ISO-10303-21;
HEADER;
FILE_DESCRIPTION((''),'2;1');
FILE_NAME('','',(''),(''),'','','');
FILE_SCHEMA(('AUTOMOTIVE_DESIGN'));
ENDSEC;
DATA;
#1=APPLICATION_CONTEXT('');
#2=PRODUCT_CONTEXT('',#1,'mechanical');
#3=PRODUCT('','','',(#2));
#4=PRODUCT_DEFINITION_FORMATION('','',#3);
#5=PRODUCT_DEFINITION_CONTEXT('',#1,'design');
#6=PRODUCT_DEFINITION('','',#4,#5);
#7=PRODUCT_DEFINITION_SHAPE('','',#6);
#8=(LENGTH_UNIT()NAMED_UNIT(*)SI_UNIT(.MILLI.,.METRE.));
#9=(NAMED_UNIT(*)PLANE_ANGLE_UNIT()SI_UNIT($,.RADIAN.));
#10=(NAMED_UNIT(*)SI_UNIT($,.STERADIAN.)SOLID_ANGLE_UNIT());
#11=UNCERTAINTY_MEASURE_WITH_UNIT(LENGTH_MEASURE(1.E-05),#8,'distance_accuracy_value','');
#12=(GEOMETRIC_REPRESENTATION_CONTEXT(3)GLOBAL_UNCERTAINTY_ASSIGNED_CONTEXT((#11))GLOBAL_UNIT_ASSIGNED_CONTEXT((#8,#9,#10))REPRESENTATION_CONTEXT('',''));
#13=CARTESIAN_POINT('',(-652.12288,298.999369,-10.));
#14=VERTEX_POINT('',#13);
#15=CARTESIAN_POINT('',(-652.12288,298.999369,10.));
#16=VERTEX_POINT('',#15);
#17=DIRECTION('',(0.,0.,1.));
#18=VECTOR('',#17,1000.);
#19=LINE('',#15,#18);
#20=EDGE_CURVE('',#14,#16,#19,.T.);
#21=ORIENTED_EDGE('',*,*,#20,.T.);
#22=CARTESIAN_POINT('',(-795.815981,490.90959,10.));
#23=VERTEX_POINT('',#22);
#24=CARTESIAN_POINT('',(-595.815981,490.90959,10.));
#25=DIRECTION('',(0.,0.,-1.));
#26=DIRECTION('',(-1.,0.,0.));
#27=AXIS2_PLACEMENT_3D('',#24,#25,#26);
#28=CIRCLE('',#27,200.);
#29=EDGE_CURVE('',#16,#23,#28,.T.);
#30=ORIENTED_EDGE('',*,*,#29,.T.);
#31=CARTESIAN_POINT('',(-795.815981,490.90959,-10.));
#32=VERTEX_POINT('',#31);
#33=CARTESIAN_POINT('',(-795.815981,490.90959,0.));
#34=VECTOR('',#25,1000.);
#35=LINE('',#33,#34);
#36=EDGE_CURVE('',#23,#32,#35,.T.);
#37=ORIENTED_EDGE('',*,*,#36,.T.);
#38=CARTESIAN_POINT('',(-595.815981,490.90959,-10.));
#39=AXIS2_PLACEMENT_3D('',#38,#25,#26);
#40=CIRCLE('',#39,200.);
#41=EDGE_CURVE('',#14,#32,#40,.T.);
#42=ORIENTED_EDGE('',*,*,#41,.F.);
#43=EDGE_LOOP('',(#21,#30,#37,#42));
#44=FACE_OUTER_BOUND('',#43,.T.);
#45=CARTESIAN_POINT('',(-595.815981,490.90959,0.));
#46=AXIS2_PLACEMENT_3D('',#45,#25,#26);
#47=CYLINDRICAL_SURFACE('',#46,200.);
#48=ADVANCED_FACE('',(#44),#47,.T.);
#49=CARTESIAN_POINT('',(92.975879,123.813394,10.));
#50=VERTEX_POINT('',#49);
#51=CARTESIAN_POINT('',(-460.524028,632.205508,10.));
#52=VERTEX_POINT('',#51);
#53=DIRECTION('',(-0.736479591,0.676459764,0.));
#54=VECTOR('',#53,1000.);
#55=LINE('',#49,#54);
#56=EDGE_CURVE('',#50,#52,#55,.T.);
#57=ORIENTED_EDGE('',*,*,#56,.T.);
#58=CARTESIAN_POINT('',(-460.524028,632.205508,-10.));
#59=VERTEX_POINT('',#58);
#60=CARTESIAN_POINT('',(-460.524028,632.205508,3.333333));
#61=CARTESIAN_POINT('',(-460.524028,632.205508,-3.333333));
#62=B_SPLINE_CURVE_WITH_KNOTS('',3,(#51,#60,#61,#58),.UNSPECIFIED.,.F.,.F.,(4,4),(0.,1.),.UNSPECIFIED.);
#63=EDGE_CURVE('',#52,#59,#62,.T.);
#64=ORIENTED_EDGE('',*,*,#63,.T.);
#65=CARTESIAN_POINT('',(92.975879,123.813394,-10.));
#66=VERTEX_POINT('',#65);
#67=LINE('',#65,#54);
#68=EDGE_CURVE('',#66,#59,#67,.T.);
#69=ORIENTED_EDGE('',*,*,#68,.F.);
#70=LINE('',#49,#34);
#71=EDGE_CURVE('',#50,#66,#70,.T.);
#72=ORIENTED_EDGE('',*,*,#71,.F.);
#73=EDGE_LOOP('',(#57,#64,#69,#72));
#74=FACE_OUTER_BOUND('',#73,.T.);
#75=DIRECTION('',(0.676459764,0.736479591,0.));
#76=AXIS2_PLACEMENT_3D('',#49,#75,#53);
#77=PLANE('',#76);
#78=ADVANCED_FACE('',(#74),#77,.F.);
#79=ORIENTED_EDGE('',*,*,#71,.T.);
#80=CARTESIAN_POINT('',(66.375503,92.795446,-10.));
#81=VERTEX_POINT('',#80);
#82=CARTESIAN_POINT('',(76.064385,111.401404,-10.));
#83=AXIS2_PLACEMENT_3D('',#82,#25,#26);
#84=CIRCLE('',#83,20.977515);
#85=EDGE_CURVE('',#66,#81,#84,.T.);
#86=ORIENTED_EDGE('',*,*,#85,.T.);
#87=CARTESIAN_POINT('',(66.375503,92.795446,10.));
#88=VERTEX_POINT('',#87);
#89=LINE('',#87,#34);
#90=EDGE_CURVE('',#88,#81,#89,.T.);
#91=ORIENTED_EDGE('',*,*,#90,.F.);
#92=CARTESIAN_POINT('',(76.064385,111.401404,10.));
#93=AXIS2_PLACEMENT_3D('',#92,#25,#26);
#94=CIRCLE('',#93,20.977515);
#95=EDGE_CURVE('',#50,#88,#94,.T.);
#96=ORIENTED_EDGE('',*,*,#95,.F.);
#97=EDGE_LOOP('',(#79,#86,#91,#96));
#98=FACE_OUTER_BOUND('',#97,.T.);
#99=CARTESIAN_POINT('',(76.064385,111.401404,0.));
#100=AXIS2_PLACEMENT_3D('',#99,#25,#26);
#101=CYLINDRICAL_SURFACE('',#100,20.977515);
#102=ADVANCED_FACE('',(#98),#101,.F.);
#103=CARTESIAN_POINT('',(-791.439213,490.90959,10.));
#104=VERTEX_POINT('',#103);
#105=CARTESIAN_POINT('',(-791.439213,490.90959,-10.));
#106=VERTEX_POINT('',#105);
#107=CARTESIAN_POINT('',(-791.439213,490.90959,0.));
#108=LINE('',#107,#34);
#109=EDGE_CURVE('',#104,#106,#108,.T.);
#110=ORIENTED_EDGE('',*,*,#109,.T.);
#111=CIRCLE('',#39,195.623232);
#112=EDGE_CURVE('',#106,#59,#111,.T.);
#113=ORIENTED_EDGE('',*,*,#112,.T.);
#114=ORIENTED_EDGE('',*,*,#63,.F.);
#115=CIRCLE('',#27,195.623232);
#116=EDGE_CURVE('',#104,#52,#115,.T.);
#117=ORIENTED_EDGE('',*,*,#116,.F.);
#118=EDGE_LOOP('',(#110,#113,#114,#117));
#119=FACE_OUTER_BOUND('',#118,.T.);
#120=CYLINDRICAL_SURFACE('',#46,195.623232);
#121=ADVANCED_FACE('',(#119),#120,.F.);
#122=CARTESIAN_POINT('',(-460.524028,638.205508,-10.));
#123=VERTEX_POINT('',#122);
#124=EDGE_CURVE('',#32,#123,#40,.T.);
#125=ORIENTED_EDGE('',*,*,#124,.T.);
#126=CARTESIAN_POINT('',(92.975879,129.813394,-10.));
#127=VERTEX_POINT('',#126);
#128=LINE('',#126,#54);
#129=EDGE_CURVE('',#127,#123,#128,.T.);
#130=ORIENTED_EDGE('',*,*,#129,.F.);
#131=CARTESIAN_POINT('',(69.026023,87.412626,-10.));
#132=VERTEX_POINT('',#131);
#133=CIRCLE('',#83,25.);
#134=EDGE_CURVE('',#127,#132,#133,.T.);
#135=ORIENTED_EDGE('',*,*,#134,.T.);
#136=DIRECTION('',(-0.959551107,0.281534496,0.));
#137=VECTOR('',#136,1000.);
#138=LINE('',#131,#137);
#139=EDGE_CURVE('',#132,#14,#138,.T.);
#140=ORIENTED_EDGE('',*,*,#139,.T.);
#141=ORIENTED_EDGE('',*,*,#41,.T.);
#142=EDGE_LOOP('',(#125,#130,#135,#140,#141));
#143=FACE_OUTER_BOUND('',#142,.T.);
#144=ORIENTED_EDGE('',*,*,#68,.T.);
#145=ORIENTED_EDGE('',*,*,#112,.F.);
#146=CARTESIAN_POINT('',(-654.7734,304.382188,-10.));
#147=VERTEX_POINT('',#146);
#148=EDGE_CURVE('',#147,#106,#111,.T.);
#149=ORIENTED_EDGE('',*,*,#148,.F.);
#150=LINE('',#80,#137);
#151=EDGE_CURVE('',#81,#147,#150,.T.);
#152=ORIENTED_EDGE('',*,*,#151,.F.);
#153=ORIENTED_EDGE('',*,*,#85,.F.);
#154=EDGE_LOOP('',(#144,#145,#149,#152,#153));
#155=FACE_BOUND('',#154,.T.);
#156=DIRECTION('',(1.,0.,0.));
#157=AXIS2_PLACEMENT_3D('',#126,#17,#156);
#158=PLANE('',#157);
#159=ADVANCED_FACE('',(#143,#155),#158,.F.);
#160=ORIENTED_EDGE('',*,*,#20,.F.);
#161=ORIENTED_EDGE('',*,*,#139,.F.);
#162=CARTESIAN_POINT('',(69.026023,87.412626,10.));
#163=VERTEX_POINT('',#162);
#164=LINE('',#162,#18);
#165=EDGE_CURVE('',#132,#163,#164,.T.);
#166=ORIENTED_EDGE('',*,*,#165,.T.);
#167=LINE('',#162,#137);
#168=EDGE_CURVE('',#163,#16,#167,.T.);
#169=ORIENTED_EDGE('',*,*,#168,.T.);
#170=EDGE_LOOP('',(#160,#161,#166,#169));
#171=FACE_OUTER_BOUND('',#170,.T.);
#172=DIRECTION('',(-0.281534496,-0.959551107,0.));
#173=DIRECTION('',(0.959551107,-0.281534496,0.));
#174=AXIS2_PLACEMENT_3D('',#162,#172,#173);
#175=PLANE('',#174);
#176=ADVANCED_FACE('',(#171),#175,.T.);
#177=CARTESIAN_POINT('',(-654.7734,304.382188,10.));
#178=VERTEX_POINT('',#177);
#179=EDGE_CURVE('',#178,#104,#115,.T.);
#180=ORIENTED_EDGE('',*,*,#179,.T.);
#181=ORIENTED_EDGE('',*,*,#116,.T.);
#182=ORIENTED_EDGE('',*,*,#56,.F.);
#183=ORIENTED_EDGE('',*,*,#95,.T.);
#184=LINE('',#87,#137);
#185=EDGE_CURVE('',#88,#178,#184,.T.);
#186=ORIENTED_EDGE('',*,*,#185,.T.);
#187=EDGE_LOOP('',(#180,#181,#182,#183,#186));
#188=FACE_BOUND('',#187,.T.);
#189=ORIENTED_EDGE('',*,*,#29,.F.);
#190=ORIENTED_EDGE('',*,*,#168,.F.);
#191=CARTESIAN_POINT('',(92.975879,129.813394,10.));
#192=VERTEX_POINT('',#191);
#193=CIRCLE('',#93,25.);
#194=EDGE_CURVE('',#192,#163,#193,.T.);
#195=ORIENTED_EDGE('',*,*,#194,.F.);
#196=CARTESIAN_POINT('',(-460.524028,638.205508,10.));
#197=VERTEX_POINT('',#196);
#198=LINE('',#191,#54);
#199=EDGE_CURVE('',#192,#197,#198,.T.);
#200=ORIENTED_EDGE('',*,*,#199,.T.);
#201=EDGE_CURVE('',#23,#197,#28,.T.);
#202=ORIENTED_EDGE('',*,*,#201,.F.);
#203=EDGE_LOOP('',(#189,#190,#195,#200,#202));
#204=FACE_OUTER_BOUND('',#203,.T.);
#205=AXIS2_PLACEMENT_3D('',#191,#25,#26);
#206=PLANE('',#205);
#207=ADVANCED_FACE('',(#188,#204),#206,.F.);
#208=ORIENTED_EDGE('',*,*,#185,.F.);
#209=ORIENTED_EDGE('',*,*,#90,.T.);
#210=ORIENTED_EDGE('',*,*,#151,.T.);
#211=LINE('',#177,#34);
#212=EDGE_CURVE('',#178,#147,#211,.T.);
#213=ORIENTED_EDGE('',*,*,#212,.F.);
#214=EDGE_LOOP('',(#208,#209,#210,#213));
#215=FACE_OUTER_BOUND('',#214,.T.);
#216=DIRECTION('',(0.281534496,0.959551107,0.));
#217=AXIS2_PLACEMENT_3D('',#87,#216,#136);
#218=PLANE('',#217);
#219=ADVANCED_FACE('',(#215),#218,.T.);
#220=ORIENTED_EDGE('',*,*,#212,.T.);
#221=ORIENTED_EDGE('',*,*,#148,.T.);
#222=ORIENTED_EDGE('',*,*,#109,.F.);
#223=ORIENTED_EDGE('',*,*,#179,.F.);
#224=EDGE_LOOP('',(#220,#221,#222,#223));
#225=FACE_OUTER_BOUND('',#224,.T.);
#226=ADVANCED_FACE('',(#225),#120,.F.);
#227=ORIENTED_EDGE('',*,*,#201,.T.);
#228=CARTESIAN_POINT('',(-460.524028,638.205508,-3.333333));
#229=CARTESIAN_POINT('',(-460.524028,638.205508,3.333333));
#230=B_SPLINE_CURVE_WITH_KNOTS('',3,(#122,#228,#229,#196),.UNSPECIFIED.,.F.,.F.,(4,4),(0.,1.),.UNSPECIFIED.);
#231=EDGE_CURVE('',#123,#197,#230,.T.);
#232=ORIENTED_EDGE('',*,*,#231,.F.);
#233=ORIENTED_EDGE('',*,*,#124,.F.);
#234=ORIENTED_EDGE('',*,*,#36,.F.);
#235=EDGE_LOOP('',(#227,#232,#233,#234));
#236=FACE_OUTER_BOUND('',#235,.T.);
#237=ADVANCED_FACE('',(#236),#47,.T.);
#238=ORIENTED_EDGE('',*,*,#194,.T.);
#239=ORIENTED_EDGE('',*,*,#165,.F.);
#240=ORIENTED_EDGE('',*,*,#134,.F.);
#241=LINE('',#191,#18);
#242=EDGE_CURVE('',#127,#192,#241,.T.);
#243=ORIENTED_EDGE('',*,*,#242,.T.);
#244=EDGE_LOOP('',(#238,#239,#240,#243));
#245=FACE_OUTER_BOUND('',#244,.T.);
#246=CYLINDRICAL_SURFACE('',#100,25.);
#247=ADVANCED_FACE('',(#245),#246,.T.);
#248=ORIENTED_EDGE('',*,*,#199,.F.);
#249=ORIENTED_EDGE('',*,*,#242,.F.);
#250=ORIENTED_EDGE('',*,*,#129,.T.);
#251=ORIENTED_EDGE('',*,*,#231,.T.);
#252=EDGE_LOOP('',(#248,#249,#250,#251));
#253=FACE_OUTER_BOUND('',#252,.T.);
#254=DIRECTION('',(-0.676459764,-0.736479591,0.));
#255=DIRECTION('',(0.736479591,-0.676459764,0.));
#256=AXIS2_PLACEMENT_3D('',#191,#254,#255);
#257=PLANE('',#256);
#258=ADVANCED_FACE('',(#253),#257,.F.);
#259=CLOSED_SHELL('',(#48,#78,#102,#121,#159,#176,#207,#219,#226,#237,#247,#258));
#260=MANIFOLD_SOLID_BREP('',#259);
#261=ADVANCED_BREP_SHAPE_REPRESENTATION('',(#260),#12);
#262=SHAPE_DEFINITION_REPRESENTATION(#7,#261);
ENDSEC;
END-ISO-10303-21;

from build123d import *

# Parameters (mm, degrees)
SKETCH2_W = 20
SKETCH2_H = 6


with BuildPart() as part:
    # Sweep1: sweep along a path in Sketch1
    with BuildLine(Plane.XY) as sweep1_path:
        Line((-460.524027919, 638.205508164), (92.975879138, 129.813393739))
        ThreePointArc((92.975879138, 129.813393739), (97.831928599, 99.10611839), (69.02602264, 87.412626283))
        Line((69.02602264, 87.412626283), (-652.122879897, 298.999368519))
        ThreePointArc((-652.122879897, 298.999368519), (-769.956329171, 589.271874597), (-460.524027919, 638.205508164))
    # Sketch2 → Sweep1 (sweep)
    with BuildSketch(Plane(origin=(-460.524027919, 0, 0), x_dir=(0, 0, -1), z_dir=(1, 0, 0))):
        with Locations((0, 635.205508164)):
            Rectangle(SKETCH2_W, SKETCH2_H)
    sweep(path=sweep1_path.line)


solid = part.part
